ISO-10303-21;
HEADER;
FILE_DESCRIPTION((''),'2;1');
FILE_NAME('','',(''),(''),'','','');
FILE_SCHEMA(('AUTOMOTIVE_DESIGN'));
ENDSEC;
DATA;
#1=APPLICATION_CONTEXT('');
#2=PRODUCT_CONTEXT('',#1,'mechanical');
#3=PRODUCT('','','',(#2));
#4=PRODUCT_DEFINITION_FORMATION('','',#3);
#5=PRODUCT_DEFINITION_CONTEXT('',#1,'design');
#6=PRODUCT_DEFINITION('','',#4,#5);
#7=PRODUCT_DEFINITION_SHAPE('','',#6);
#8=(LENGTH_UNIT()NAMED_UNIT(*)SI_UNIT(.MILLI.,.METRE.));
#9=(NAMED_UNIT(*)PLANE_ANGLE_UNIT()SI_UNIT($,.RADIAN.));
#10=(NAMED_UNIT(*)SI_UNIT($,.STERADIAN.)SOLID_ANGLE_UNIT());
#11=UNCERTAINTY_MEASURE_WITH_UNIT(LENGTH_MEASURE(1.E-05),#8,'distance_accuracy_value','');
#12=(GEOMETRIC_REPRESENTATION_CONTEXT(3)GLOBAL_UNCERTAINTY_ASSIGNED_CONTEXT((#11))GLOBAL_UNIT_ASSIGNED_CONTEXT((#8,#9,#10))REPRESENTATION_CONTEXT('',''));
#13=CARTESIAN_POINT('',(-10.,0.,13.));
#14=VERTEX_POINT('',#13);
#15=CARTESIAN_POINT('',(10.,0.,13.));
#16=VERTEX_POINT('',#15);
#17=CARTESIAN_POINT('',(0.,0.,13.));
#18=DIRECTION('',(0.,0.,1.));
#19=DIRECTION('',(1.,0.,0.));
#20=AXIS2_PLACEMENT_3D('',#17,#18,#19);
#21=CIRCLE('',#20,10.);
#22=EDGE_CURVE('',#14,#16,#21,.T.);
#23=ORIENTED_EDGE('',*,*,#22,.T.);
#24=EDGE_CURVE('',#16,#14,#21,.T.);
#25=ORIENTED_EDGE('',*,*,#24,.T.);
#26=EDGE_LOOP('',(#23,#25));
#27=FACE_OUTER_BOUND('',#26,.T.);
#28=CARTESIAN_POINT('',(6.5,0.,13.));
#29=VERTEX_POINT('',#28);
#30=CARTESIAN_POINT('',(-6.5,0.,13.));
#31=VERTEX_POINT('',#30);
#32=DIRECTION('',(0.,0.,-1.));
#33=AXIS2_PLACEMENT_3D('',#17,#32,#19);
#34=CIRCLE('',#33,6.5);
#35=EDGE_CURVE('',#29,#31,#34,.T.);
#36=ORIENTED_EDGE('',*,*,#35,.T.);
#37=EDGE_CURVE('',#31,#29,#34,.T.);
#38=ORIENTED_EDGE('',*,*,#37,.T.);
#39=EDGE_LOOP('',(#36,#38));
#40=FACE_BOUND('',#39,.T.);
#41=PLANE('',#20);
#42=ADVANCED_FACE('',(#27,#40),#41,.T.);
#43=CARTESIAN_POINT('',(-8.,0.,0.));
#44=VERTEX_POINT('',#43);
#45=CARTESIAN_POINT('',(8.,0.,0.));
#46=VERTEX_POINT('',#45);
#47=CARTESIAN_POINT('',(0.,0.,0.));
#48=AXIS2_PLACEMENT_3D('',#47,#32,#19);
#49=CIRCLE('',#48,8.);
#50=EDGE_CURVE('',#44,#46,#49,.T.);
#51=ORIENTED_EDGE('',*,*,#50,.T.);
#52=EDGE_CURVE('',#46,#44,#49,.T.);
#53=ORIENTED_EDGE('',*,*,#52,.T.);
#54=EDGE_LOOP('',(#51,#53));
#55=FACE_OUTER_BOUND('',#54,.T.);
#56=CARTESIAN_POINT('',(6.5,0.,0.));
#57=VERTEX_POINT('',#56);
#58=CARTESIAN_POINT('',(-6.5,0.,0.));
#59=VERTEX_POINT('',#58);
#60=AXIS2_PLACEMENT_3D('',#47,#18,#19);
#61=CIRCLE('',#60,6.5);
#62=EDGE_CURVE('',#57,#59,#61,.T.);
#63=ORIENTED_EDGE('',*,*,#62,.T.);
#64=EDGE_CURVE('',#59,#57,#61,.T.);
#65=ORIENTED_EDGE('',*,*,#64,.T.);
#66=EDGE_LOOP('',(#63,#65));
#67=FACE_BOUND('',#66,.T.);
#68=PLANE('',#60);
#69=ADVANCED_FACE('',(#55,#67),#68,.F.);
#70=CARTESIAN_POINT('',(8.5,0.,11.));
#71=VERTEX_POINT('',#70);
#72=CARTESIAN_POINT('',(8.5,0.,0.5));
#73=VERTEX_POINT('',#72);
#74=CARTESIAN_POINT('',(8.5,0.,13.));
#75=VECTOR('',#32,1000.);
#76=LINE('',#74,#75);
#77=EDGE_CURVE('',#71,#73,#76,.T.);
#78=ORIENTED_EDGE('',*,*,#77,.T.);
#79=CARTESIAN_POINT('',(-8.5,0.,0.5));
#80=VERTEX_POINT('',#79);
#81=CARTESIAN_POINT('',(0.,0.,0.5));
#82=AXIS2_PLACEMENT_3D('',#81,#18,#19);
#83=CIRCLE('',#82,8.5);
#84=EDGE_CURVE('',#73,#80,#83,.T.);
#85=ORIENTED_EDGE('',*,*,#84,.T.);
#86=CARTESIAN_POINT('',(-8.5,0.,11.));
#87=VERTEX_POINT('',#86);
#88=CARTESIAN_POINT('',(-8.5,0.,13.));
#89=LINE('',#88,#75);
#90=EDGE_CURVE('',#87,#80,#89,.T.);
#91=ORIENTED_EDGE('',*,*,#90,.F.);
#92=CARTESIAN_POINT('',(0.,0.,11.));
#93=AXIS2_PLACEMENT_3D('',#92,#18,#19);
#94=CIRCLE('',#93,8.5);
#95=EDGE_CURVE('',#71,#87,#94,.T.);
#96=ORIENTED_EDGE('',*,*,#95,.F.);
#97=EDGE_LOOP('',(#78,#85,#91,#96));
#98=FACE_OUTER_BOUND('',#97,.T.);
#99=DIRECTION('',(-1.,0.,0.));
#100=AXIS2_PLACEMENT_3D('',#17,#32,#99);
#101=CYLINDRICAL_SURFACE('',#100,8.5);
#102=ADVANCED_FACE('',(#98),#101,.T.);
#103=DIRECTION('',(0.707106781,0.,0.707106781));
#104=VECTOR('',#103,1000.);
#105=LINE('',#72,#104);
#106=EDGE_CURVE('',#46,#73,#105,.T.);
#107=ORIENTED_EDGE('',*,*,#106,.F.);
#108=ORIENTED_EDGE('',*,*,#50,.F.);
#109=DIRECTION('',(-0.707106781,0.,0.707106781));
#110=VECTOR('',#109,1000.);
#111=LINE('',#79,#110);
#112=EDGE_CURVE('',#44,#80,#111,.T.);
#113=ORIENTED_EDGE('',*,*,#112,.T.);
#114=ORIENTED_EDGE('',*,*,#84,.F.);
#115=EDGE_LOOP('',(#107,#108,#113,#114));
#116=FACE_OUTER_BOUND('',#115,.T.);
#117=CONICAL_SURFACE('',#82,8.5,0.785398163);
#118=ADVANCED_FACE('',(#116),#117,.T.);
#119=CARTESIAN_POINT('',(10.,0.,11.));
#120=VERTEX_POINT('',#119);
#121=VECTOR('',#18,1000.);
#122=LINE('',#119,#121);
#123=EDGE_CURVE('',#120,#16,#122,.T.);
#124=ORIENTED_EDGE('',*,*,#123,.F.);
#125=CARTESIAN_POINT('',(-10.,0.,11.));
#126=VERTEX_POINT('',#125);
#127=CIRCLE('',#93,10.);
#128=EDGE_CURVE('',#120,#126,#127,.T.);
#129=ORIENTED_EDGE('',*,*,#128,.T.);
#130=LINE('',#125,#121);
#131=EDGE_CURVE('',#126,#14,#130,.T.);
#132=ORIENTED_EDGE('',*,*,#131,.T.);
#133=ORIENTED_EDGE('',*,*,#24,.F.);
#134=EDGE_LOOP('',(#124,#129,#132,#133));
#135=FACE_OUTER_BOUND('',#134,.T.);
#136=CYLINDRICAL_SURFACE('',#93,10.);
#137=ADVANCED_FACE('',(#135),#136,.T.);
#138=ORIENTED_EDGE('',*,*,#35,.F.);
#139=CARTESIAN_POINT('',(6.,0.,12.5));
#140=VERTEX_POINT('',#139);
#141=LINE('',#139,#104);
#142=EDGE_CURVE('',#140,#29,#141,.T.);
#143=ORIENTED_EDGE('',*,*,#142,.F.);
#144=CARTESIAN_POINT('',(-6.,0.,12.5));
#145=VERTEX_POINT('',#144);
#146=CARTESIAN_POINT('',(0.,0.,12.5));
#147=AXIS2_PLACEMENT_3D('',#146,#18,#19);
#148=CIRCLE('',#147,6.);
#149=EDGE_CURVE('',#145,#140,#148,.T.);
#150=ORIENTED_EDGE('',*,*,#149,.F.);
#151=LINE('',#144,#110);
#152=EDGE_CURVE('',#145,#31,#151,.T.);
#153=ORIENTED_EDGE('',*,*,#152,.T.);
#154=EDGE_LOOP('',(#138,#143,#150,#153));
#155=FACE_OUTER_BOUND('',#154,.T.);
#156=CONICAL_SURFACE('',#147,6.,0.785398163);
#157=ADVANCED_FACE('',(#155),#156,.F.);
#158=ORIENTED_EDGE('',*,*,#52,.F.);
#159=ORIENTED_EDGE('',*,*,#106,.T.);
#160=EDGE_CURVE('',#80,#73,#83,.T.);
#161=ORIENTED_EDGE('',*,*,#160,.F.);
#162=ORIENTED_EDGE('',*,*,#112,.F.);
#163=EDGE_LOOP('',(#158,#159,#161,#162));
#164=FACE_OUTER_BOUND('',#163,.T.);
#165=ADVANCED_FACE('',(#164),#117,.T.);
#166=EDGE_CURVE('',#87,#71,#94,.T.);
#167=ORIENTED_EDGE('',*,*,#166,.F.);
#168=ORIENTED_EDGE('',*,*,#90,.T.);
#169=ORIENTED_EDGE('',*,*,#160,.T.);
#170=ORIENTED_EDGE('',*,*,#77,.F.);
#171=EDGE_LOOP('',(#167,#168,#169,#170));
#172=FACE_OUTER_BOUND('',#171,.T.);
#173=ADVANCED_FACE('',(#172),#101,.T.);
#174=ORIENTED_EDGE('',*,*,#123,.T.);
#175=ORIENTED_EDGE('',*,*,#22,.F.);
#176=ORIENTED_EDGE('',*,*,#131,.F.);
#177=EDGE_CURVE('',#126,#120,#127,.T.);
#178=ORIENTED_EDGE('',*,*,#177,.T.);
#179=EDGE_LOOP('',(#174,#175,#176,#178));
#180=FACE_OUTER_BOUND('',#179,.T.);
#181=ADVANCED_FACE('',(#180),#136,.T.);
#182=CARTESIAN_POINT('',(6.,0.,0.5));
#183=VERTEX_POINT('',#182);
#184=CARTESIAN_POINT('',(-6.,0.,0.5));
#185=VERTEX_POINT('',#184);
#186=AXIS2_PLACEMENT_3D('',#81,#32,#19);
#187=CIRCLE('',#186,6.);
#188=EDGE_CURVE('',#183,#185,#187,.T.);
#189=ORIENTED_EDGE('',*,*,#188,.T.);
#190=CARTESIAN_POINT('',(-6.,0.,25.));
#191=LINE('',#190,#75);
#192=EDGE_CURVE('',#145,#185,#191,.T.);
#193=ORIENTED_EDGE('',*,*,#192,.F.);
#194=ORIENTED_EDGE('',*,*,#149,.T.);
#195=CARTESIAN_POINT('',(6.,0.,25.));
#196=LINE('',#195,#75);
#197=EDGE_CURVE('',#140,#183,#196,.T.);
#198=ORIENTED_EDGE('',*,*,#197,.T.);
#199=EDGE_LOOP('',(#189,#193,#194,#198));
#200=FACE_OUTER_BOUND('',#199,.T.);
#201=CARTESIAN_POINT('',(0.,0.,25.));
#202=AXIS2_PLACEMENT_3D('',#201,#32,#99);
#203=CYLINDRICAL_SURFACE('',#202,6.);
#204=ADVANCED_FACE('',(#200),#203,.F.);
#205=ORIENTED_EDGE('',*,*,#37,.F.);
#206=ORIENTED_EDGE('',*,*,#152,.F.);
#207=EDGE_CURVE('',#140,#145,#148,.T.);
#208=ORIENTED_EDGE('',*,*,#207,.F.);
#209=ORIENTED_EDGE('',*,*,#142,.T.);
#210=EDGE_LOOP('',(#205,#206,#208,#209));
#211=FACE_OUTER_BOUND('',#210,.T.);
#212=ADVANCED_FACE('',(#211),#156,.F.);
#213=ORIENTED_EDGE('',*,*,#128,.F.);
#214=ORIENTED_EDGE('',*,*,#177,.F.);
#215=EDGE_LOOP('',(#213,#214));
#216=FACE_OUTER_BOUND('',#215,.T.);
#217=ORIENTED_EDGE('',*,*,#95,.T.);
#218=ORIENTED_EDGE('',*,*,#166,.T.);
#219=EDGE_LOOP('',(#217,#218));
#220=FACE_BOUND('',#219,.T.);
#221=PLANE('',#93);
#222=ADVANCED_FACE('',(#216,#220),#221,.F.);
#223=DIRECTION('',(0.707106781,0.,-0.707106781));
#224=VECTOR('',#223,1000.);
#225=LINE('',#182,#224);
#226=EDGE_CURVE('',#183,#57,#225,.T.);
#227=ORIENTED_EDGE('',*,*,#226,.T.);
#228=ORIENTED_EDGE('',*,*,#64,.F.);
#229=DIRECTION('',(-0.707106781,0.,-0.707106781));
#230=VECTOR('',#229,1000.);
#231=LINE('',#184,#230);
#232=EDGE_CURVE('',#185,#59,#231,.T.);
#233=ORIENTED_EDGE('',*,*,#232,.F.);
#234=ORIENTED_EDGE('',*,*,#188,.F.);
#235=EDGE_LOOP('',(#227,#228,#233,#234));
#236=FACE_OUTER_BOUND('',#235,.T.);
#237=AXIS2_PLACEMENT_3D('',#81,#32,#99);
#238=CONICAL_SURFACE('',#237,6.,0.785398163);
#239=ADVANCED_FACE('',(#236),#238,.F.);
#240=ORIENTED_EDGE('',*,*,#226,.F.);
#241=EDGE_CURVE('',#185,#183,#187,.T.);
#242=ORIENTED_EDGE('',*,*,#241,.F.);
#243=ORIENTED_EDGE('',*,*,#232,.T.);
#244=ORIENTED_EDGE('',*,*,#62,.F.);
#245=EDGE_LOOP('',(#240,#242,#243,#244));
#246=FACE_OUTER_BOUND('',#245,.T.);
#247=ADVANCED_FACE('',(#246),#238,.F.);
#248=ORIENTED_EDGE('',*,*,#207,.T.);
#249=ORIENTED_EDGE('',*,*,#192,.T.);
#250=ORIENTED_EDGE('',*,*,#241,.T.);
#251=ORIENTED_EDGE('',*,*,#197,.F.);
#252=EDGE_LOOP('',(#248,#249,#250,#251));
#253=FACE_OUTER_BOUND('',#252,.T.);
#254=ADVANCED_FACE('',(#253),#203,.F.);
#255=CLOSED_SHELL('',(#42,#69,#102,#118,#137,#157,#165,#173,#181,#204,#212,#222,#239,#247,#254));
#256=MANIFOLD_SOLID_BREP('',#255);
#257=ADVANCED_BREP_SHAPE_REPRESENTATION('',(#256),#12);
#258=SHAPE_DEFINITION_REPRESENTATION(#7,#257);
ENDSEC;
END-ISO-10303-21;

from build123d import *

# Parameters (mm, degrees)
SKETCH1_R           = 8.5
BOSS_EXTRUDE1_DEPTH = 13
SKETCH2_R           = 10
BOSS_EXTRUDE2_DEPTH = 2
SKETCH3_R           = 6
CUT_EXTRUDE1_DEPTH  = 25
CHAMFER1_SIZE       = 0.5


with BuildPart() as part:
    # Sketch1 → Boss-Extrude1 (new body)
    with BuildSketch(Plane.XY):
        with Locations(Location((0, 0, 0), (0, 0, 180))):
            Circle(SKETCH1_R)
    extrude(amount=BOSS_EXTRUDE1_DEPTH)

    # Sketch2 → Boss-Extrude2 (add)
    with BuildSketch(Plane.XY.offset(13)):
        Circle(SKETCH2_R)
    extrude(amount=-BOSS_EXTRUDE2_DEPTH)

    # Sketch3 → Cut-Extrude1 (cut)
    with BuildSketch(Plane(origin=(0, 0, 0), x_dir=(-1, 0, 0), z_dir=(0, 0, -1))):
        Circle(SKETCH3_R)
    extrude(amount=-CUT_EXTRUDE1_DEPTH, mode=Mode.SUBTRACT)

    # Chamfer1
    chamfer1_edges = [part.edges().sort_by_distance(p)[0] for p in [
        (6, 0, 13),
        (6, 0, 0),
        (8.5, 0, 0),
    ]]
    chamfer(chamfer1_edges, length=CHAMFER1_SIZE)


solid = part.part
